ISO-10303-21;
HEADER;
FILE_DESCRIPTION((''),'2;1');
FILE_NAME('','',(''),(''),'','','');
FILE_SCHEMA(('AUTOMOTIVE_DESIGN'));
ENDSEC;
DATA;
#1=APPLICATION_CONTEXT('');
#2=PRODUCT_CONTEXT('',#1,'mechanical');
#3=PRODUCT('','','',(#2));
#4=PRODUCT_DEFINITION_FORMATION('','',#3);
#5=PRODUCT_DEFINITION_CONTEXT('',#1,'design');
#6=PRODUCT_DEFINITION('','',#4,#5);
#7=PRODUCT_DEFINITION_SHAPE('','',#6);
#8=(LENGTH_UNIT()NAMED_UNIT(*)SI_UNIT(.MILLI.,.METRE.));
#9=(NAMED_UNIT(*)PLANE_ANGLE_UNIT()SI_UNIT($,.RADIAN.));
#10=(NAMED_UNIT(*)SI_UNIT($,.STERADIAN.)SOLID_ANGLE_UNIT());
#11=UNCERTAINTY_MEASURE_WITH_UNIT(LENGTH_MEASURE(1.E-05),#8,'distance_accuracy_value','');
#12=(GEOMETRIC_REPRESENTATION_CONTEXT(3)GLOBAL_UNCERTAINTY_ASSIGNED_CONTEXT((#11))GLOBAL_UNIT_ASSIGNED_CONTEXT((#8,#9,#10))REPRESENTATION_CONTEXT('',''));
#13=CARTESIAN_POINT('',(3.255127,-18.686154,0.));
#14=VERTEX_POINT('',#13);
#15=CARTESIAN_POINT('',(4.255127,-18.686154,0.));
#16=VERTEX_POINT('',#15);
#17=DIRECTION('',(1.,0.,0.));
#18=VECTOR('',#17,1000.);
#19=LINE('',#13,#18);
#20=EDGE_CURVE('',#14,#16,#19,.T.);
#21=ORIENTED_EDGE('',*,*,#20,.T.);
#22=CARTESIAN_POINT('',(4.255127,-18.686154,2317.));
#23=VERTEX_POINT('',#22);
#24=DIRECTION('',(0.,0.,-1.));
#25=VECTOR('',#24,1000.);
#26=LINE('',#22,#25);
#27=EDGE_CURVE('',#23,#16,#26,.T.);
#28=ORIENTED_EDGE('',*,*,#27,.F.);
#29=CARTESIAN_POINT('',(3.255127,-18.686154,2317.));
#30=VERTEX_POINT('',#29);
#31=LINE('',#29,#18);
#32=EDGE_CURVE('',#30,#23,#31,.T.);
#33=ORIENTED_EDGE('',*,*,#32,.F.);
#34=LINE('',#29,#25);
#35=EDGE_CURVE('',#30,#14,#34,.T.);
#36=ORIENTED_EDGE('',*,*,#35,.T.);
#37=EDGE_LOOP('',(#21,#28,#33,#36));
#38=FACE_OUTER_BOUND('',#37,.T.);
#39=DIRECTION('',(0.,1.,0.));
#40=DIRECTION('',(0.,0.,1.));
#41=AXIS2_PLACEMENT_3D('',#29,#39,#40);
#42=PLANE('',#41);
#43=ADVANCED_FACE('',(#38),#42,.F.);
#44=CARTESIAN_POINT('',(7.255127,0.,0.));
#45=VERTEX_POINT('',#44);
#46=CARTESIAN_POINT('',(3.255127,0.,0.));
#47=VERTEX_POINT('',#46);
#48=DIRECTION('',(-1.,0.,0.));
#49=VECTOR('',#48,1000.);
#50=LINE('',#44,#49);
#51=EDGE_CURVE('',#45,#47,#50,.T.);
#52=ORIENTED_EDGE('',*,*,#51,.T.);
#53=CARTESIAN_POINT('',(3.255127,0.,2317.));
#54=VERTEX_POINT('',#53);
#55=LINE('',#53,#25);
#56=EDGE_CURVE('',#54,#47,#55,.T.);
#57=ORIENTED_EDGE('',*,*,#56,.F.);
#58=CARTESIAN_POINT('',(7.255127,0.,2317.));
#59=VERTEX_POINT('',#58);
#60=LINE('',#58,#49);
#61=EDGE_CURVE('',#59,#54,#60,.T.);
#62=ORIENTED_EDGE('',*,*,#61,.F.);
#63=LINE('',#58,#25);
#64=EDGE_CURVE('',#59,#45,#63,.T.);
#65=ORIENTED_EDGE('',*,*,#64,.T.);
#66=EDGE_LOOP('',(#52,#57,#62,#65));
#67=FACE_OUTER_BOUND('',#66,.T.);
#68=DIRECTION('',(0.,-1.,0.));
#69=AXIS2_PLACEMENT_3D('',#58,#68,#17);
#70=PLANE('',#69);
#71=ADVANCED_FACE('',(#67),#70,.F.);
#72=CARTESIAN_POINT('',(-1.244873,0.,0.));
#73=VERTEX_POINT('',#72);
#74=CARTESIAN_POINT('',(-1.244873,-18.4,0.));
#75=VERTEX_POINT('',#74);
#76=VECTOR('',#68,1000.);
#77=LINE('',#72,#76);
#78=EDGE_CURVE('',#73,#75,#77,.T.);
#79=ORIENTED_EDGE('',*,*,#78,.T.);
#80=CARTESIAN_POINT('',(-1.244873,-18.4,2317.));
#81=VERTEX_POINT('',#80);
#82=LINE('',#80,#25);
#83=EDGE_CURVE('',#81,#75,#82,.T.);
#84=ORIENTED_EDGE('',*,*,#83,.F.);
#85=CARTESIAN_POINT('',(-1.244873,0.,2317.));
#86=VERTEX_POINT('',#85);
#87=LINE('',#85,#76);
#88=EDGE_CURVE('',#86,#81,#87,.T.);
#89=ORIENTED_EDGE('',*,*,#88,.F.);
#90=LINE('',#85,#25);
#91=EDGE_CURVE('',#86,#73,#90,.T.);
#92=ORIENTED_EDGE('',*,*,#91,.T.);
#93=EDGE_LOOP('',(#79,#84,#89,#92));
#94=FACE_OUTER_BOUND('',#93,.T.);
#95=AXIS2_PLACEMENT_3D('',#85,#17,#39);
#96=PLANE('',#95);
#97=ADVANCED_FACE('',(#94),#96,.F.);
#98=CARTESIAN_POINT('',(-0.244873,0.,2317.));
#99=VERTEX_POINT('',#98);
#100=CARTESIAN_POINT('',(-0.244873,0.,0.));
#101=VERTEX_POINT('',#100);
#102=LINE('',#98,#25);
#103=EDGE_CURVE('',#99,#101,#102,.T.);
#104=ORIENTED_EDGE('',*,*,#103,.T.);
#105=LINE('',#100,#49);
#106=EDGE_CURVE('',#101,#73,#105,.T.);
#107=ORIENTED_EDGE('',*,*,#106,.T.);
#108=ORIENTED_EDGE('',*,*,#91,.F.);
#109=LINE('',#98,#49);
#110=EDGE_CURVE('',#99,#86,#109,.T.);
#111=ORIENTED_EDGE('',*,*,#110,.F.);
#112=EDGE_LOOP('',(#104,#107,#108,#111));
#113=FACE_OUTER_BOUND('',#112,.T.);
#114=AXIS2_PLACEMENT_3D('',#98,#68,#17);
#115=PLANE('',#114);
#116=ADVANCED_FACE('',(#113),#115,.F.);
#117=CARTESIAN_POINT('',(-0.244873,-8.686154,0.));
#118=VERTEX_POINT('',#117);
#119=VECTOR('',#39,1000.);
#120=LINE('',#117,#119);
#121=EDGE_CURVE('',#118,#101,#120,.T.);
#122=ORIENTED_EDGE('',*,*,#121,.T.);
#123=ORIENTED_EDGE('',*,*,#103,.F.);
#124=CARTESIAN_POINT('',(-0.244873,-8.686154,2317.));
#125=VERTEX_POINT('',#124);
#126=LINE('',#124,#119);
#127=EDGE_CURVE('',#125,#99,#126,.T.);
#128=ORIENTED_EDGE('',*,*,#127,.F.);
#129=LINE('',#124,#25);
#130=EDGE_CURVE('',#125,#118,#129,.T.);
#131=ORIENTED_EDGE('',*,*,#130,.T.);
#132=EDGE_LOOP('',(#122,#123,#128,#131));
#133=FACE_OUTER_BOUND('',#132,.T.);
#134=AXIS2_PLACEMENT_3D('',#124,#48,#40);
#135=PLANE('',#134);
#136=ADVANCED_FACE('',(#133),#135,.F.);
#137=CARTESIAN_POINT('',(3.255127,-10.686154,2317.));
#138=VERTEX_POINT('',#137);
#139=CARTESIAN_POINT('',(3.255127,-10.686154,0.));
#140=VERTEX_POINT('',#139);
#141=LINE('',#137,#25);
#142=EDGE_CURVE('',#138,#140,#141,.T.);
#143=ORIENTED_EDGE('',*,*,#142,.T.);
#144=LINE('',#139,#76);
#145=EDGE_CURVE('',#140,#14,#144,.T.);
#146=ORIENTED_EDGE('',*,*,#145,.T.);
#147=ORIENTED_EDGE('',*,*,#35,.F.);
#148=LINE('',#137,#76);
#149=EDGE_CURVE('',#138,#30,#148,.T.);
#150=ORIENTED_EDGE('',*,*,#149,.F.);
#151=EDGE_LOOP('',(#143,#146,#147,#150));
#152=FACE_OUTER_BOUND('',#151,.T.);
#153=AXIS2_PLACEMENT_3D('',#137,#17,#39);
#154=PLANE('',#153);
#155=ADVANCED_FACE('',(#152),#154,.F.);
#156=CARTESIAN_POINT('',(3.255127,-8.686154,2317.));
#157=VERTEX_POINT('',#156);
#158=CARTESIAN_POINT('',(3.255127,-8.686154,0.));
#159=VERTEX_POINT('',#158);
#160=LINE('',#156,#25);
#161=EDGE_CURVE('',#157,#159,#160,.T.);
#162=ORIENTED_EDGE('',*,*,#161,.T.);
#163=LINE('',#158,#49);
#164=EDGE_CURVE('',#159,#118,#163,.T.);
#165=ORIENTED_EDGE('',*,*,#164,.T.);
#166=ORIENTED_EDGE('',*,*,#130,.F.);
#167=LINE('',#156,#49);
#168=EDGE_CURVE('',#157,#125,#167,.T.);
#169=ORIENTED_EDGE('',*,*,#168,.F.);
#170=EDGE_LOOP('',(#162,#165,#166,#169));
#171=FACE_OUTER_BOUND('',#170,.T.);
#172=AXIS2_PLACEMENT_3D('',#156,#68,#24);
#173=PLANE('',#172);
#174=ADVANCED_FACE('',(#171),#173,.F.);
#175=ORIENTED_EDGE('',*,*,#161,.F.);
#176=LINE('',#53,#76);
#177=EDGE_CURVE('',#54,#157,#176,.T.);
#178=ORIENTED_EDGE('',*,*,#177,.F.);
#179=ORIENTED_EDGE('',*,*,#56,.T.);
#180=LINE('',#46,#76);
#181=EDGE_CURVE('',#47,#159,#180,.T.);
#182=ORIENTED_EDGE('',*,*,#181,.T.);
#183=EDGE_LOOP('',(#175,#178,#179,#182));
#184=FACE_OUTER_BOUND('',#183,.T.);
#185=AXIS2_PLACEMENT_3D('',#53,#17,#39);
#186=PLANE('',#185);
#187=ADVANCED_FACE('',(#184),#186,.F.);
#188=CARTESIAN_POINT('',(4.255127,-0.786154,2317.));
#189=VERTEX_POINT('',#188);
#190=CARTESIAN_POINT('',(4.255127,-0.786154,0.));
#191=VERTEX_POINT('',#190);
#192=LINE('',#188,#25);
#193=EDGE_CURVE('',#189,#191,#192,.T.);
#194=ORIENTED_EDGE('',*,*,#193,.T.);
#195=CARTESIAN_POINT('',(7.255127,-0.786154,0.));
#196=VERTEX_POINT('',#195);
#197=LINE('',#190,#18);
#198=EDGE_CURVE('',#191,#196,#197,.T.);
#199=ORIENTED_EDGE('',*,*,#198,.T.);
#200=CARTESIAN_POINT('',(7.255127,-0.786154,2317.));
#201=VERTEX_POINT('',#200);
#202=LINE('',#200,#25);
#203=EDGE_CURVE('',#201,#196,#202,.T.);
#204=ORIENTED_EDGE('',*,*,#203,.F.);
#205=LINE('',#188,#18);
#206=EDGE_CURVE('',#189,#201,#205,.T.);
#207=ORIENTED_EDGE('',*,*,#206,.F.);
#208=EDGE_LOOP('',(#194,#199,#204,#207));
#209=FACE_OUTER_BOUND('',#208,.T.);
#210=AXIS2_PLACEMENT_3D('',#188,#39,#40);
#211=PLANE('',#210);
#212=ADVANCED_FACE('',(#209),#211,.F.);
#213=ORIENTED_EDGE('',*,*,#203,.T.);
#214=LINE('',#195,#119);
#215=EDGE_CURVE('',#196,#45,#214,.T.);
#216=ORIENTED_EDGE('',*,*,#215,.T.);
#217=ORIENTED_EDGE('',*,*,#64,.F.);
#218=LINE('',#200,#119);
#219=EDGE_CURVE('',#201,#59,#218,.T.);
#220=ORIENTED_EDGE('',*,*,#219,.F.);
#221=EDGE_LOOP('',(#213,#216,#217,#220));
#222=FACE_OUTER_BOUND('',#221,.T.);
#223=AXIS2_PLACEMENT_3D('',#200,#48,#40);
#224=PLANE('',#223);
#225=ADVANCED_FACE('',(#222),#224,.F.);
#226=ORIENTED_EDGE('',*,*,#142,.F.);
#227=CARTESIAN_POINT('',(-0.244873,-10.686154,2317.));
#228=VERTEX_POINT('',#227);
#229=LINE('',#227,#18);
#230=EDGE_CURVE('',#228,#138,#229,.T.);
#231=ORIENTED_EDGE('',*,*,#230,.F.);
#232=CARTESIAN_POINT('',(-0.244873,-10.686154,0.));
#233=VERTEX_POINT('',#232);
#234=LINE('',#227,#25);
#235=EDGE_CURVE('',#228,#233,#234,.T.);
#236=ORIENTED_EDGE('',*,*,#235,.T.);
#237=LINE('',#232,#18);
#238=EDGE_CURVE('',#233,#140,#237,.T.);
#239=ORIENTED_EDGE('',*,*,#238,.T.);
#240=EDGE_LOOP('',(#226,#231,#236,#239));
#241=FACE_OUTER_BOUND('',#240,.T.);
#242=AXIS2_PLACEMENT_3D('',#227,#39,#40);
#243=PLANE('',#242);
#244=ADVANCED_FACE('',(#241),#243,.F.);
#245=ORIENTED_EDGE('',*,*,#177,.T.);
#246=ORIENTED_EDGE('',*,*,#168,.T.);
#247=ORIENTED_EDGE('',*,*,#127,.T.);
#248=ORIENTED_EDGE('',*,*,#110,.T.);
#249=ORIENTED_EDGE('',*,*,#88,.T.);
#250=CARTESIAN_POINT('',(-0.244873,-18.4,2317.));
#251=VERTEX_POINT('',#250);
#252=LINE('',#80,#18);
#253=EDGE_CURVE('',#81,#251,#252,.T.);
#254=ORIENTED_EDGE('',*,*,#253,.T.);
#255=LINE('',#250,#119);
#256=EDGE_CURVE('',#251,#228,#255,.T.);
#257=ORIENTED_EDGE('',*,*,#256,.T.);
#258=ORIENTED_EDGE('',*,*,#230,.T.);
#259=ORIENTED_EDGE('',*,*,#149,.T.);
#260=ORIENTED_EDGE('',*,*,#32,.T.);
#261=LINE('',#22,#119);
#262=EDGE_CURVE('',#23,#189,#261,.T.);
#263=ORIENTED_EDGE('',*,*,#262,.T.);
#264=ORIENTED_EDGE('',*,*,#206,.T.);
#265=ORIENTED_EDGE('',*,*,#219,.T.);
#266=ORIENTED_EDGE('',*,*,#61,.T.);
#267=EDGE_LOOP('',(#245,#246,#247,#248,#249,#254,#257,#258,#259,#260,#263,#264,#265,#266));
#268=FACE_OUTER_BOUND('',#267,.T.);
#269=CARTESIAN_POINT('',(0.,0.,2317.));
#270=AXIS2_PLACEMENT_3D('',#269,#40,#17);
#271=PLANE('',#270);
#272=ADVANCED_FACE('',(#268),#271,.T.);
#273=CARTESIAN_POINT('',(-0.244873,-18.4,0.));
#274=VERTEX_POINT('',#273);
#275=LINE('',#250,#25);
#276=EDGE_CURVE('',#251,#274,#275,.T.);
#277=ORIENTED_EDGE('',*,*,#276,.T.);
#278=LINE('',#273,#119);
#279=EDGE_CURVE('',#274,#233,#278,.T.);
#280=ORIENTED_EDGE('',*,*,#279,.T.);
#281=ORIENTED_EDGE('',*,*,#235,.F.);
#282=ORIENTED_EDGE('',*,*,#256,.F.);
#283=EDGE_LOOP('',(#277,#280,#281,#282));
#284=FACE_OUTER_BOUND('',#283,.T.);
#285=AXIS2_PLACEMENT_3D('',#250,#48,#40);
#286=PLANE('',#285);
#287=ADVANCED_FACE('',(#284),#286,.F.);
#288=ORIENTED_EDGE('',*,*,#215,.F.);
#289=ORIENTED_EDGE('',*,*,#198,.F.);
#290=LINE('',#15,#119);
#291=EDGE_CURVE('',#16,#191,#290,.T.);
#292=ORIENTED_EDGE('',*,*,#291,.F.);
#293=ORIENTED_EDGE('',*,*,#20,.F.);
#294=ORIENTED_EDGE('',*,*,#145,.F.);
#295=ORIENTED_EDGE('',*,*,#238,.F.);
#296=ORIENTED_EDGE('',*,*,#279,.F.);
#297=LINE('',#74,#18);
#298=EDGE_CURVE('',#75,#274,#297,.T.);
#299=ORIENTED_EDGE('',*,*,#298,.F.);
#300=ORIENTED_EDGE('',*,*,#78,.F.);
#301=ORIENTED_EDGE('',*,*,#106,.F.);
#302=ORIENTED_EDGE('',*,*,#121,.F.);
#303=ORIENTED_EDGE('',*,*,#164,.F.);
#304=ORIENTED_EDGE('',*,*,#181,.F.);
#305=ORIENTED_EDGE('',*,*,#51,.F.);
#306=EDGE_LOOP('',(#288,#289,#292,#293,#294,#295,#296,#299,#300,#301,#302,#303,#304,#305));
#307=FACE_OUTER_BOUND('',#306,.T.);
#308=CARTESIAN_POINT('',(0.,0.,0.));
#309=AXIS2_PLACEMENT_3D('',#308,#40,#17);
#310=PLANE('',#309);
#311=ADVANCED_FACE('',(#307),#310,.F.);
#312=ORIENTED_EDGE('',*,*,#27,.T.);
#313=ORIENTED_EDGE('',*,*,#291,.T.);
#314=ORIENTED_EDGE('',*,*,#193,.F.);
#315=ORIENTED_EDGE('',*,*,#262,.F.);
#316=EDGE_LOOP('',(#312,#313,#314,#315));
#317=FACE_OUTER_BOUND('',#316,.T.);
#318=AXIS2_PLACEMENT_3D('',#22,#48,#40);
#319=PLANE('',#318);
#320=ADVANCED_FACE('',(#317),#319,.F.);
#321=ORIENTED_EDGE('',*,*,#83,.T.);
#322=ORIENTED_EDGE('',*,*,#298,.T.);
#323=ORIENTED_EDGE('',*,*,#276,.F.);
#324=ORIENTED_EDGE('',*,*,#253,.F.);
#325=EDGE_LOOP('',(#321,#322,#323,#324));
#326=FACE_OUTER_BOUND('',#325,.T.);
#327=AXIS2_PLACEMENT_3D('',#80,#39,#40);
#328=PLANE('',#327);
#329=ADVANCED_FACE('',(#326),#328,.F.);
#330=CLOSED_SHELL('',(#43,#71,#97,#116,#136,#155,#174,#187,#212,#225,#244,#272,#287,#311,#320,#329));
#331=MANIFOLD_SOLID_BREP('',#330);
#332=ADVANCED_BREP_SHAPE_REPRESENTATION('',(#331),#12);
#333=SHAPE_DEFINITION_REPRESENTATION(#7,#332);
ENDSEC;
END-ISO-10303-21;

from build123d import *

# Parameters (mm, degrees)
EXTRUDE_1_DEPTH = 2317


with BuildPart() as part:
    # 草图1 → 凸台-拉伸1 (new body)
    with BuildSketch(Plane.XY):
        Polygon((7.255126662, 0), (3.255126662, 0), (3.255126662, -8.686153846), (-0.244873338, -8.686153846), (-0.244873338, 0), (-1.244873338, 0), (-1.244873338, -18.4), (-0.244873338, -18.4), (-0.244873338, -10.686153846), (3.255126662, -10.686153846), (3.255126662, -18.686153846), (4.255126662, -18.686153846), (4.255126662, -0.786153846), (7.255126662, -0.786153846), align=None)
    extrude(amount=EXTRUDE_1_DEPTH)


solid = part.part
